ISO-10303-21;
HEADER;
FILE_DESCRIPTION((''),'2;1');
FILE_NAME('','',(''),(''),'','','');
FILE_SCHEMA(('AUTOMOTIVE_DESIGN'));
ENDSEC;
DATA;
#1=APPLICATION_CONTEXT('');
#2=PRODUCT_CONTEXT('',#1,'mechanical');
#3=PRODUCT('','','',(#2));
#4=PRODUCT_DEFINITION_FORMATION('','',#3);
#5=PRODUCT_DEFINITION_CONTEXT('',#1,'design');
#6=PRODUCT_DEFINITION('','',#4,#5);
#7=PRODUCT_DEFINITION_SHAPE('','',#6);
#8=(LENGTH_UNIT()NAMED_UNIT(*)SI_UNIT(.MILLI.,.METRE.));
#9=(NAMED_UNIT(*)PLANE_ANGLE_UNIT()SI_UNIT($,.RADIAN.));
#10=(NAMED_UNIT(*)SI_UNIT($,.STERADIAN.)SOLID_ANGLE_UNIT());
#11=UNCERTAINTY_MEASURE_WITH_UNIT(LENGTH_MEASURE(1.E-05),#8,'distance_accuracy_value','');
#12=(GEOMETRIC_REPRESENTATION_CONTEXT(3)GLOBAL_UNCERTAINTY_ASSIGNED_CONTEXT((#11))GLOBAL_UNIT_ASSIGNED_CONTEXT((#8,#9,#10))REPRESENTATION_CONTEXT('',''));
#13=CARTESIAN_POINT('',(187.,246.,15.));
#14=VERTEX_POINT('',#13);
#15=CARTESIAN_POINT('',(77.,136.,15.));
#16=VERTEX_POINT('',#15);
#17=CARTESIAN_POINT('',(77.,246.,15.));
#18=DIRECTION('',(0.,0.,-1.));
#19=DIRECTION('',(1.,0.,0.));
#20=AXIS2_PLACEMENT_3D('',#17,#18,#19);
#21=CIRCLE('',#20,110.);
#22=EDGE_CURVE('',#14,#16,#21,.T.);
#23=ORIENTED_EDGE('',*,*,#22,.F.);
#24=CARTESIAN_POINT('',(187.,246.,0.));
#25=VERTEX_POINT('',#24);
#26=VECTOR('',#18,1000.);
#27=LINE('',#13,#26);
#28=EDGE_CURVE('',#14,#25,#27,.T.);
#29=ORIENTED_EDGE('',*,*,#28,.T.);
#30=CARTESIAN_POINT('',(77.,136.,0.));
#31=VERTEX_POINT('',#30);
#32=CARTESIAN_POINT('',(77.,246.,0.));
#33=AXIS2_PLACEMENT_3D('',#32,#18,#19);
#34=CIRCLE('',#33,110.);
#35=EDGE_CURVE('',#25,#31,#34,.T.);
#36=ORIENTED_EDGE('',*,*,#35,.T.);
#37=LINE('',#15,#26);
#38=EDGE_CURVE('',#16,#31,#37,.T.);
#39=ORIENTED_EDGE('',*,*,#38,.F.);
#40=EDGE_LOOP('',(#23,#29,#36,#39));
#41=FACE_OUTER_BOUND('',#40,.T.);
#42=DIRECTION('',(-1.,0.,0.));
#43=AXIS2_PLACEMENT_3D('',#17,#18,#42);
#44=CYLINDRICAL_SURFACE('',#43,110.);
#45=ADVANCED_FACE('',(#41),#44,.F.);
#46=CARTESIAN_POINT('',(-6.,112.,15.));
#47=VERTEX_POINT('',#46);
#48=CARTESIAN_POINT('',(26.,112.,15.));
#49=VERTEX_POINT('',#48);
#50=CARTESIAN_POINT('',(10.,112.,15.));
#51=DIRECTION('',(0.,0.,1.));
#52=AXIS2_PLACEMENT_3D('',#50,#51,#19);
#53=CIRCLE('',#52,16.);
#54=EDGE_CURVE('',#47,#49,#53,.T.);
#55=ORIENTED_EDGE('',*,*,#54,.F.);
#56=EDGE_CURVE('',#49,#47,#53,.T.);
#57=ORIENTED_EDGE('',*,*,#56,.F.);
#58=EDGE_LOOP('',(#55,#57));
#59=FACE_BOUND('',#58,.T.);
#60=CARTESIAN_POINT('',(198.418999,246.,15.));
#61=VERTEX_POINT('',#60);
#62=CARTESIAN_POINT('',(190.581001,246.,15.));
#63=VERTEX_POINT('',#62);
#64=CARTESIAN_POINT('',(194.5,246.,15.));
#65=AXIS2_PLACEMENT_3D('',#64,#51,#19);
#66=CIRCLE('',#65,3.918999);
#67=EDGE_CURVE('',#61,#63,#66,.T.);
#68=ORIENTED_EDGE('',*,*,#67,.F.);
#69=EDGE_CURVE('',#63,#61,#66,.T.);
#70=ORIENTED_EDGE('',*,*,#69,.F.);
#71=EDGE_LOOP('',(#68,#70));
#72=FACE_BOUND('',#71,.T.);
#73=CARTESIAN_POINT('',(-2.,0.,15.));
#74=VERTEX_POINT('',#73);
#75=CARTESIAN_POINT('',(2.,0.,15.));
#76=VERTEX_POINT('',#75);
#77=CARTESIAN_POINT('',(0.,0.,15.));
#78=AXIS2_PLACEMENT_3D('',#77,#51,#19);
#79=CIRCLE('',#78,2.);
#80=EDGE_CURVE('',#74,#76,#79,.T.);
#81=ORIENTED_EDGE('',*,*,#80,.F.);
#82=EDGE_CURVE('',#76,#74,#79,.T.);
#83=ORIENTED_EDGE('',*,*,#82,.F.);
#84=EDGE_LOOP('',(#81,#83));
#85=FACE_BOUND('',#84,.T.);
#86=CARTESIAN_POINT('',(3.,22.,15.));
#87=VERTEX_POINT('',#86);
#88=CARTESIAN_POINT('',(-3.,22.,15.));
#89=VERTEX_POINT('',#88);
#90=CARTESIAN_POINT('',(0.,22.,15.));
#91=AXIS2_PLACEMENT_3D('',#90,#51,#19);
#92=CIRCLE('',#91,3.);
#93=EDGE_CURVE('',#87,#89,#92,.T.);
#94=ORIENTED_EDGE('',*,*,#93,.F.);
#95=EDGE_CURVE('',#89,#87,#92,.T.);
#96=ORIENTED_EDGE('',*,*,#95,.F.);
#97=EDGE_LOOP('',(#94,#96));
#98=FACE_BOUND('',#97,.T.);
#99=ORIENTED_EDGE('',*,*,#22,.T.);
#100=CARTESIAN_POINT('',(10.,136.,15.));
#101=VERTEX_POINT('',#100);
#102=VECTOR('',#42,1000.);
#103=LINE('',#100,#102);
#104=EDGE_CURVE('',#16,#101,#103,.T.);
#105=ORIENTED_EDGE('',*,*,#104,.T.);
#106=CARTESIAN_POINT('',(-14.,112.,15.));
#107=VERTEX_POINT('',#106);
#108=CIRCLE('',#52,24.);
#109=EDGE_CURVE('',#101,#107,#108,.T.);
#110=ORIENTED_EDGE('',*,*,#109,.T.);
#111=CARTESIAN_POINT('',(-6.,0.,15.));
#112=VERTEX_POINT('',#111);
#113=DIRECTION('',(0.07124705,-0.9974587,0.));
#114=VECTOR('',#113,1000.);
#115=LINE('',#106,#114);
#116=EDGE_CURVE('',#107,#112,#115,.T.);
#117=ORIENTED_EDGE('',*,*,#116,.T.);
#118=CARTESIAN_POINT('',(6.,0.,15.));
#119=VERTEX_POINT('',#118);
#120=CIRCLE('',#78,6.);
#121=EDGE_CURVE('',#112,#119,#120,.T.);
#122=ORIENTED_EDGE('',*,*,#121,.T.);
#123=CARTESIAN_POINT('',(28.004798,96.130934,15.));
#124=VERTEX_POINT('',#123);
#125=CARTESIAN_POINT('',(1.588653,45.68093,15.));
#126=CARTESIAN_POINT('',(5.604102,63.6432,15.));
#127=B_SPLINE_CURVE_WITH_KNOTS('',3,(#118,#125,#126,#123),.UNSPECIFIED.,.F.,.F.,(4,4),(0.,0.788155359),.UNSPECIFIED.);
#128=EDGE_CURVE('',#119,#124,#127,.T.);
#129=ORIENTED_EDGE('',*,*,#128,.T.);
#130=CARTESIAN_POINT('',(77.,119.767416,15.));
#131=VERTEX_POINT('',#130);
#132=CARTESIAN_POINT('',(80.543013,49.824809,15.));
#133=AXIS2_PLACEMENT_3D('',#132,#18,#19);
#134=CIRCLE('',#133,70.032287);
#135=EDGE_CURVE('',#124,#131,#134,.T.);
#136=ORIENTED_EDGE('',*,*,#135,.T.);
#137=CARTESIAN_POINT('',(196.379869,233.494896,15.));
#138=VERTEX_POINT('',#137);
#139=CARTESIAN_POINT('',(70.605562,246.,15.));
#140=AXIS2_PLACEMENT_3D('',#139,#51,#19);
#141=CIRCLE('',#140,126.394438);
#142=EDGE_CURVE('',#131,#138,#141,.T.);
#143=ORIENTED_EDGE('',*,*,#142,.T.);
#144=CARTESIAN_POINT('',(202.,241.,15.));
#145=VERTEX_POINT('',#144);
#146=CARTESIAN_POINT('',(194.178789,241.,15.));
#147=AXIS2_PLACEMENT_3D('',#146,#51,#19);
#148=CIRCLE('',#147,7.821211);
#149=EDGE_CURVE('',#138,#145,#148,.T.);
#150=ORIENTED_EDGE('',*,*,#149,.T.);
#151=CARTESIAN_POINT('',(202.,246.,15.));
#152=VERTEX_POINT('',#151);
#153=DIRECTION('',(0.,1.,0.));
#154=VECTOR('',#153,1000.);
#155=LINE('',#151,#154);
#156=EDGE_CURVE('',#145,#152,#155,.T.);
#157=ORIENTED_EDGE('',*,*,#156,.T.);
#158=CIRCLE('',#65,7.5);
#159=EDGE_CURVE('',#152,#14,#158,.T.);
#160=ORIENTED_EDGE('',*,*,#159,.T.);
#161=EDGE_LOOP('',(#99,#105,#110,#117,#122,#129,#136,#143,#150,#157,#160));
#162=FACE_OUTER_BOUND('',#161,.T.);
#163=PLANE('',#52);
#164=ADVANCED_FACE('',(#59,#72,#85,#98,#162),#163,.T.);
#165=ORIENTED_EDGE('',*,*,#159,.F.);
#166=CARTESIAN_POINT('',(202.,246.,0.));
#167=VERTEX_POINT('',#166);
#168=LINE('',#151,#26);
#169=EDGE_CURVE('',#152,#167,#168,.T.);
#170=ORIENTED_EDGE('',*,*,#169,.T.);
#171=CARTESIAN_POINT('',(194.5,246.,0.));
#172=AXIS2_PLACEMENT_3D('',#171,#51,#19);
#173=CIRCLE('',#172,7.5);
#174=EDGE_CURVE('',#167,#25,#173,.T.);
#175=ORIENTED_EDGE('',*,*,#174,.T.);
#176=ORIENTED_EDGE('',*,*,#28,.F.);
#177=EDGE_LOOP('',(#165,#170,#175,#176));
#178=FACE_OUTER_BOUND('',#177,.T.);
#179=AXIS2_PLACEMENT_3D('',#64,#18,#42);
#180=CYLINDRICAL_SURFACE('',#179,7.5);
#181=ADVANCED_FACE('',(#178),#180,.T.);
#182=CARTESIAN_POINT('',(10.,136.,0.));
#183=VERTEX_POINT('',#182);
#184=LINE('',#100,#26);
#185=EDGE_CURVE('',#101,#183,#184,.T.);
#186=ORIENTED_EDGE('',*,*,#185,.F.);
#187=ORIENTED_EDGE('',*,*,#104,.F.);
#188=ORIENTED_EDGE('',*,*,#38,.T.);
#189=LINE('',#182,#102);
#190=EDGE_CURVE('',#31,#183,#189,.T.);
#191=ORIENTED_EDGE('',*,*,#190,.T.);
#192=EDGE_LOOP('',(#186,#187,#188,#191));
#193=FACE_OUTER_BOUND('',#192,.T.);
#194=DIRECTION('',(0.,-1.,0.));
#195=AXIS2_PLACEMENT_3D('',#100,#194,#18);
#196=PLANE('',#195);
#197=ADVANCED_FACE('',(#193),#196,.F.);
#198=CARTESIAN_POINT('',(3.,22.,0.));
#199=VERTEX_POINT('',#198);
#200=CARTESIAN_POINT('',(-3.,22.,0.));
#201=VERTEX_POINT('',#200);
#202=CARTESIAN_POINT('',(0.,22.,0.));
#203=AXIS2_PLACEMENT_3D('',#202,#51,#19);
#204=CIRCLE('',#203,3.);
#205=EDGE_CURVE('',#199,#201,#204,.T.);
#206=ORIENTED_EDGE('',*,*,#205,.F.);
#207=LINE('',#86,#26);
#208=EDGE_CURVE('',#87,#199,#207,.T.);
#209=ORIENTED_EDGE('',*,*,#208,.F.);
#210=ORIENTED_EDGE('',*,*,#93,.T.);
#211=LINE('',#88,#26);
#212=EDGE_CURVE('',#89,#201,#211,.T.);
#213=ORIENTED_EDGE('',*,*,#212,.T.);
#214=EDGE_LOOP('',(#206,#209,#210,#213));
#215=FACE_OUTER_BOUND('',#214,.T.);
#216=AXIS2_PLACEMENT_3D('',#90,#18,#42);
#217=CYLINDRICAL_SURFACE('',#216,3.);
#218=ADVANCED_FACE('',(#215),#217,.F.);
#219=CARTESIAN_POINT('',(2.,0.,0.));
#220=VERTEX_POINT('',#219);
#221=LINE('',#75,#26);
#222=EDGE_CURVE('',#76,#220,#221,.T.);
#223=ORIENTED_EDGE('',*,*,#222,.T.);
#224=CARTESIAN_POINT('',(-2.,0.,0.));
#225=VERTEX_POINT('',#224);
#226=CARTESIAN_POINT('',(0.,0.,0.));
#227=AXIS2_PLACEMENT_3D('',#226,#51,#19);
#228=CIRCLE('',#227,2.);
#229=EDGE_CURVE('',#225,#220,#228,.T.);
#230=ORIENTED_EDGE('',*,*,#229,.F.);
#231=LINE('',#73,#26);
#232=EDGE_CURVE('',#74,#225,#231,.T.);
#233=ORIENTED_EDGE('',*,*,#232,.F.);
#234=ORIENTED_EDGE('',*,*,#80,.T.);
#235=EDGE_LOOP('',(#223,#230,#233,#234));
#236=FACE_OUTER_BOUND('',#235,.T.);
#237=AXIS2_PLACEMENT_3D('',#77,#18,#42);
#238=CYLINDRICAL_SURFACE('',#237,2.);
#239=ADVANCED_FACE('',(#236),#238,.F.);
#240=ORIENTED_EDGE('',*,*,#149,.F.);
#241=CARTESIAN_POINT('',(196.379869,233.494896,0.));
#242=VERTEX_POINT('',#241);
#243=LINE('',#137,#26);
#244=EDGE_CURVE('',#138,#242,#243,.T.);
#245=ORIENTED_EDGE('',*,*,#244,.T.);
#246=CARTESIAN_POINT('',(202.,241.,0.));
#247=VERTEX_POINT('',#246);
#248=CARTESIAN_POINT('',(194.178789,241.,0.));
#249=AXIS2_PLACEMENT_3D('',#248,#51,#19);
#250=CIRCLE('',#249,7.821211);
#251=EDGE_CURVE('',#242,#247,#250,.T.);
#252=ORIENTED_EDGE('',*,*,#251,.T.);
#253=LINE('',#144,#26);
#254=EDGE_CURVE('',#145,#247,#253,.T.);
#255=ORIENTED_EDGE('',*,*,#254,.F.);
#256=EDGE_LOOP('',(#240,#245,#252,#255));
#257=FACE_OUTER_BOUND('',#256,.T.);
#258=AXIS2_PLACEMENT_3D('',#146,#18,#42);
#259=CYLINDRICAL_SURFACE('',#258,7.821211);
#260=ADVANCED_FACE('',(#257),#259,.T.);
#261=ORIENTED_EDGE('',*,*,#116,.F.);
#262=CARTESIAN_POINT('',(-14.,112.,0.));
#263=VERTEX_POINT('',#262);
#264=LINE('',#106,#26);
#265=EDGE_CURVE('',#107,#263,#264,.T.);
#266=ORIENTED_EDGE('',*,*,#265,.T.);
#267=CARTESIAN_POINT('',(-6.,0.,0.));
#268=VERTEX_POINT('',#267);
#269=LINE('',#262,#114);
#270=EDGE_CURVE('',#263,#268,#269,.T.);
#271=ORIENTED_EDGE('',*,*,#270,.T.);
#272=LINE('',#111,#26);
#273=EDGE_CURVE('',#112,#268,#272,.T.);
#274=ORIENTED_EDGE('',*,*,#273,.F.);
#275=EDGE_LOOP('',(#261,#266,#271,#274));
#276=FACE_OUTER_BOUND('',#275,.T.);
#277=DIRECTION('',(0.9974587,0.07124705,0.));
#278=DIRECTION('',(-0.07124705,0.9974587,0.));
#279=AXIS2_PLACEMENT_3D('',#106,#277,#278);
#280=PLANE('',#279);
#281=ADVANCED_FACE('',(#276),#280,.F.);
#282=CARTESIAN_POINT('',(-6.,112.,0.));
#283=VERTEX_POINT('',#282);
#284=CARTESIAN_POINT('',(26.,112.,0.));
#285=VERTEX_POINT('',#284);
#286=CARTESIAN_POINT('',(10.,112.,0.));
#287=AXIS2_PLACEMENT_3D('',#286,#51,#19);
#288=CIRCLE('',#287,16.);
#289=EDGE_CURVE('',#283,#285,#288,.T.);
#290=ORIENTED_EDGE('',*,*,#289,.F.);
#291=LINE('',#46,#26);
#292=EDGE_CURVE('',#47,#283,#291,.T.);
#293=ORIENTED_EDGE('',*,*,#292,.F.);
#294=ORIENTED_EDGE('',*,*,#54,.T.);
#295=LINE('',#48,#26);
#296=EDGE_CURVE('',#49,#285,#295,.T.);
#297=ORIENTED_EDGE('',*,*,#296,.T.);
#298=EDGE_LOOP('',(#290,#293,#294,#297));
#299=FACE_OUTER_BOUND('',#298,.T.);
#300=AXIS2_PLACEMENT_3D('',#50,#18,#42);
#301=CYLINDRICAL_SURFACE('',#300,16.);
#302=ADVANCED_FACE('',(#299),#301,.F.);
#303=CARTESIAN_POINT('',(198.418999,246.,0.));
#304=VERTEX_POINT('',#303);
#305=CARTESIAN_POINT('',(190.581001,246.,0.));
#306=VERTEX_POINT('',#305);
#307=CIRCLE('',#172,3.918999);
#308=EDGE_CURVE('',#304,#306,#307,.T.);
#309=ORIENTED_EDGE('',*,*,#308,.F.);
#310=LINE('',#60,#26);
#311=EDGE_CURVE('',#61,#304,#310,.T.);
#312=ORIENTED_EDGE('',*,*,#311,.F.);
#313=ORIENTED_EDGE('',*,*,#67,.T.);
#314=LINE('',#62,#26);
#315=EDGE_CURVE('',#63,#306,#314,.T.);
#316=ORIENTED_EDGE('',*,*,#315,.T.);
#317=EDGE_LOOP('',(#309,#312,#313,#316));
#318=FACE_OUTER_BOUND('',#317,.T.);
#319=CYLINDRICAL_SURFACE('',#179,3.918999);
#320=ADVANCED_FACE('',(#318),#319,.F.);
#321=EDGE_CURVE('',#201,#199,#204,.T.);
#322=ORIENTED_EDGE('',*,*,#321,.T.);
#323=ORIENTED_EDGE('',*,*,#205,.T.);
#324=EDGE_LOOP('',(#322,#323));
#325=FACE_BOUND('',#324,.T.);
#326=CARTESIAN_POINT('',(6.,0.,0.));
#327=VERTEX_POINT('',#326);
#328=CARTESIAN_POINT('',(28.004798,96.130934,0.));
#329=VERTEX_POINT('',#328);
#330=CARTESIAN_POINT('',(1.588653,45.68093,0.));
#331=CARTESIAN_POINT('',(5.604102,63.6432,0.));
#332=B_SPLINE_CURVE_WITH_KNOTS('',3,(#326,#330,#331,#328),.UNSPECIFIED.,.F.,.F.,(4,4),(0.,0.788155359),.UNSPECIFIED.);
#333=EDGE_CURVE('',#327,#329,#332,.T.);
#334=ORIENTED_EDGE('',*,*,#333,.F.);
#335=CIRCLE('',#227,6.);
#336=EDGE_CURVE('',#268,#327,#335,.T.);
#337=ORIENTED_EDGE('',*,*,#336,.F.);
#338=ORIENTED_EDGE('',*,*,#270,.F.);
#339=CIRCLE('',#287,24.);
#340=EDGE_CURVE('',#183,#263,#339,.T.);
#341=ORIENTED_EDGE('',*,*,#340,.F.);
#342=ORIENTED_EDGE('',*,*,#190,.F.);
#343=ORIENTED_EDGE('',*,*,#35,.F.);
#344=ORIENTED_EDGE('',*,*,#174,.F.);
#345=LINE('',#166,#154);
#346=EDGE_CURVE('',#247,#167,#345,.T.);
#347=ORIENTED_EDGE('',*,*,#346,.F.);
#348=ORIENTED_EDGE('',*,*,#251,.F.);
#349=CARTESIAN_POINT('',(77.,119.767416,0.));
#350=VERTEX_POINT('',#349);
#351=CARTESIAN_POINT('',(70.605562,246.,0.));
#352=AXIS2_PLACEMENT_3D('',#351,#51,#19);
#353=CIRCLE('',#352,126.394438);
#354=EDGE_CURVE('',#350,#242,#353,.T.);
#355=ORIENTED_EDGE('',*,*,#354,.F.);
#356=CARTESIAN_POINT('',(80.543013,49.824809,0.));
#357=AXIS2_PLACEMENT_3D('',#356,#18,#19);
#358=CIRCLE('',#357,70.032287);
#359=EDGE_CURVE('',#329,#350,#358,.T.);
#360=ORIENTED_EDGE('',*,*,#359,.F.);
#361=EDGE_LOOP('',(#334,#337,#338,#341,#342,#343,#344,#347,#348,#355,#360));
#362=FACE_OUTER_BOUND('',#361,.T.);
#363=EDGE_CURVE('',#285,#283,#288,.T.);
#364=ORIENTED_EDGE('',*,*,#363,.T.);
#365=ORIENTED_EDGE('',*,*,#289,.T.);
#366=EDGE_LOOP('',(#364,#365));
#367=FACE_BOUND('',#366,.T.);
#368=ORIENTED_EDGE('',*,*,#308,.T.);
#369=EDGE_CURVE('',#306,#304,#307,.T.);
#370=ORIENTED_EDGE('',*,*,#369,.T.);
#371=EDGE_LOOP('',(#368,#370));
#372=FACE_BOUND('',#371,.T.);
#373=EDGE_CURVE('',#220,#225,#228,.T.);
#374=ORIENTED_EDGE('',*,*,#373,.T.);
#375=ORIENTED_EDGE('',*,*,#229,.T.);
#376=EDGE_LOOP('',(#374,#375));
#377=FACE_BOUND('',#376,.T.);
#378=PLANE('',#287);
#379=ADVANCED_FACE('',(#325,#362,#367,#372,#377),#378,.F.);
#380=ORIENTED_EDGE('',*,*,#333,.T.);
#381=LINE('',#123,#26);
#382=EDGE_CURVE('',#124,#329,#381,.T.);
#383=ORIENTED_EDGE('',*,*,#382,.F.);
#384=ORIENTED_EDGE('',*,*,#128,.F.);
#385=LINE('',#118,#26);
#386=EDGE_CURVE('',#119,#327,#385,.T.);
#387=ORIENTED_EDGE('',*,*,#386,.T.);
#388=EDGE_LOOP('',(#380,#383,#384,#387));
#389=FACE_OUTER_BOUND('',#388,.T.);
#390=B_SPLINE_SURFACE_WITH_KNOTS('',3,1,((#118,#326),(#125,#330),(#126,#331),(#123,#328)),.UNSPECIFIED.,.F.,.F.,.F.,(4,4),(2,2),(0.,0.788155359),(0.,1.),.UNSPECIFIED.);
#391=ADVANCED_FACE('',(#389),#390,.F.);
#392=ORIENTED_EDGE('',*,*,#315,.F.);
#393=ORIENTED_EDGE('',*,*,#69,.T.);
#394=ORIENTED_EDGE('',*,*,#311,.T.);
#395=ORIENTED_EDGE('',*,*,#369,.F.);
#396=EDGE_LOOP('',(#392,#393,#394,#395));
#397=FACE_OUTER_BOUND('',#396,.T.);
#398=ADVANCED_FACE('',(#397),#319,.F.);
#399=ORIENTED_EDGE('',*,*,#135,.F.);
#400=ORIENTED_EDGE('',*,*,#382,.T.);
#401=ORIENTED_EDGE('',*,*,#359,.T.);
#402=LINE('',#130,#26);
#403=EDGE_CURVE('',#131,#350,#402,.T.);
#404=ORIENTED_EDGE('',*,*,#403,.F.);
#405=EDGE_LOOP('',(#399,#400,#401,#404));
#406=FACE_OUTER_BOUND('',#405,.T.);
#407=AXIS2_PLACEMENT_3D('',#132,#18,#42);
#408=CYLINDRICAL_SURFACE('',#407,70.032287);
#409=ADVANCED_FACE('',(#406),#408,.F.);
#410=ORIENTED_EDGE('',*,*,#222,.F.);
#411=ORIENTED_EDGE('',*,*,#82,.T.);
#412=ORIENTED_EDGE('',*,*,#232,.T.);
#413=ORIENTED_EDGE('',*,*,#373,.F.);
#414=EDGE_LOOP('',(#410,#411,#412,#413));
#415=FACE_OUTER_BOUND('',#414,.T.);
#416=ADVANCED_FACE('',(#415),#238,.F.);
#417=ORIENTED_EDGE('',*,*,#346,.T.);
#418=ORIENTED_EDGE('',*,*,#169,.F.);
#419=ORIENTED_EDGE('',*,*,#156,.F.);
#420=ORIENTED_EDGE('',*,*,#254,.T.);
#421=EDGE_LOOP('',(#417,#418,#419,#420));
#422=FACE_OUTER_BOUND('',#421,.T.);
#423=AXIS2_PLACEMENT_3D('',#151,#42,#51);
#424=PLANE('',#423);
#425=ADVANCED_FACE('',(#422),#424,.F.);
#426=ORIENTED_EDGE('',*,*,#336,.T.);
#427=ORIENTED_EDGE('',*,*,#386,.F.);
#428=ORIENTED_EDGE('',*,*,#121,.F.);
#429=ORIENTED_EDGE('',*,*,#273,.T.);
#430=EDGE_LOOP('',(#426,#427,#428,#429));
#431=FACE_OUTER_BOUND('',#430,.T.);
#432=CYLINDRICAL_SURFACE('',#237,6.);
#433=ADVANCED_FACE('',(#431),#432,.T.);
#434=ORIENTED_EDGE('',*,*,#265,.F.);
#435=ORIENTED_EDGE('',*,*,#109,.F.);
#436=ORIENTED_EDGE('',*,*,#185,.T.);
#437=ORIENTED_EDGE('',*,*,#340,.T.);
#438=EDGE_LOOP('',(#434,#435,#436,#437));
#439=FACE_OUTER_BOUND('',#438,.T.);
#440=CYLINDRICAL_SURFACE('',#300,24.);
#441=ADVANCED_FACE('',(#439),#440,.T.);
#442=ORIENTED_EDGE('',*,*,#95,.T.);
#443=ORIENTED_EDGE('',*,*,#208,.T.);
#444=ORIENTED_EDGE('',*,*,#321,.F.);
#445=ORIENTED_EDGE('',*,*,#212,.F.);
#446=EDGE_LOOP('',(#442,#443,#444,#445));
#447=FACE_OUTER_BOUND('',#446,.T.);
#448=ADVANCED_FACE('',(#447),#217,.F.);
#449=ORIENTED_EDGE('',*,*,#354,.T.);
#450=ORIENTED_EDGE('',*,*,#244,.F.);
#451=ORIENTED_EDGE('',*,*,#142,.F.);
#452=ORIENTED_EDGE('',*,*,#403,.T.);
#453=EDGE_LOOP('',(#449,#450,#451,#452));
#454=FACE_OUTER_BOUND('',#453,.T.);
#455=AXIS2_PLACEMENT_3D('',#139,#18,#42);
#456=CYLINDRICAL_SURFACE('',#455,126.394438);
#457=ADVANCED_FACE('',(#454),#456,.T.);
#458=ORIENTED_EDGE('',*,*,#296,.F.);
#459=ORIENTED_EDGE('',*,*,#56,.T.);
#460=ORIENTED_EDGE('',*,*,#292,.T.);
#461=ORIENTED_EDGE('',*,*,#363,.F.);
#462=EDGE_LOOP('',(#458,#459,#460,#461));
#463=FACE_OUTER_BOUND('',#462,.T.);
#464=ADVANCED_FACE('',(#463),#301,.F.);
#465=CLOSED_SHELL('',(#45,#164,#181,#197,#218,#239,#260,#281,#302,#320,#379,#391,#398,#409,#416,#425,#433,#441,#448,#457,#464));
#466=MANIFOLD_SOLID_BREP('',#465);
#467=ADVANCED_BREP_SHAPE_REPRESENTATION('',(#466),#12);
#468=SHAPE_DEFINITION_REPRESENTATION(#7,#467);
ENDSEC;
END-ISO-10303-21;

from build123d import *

# Parameters (mm, degrees)
SKETCH_1_R      = 2
SKETCH_1_R_2    = 16
SKETCH_1_R_3    = 3.91899873
SKETCH_1_R_4    = 3
EXTRUDE_1_DEPTH = 15


with BuildPart() as part:
    # 草图1 → 凸台-拉伸1 (new body)
    with BuildSketch(Plane.XY):
        with BuildLine():
            Line((-14, 112), (-6, 0))
            ThreePointArc((-6, 0), (0, -6), (6, 0))
            add(Edge.make_bspline(
                [(6, 0), (1.588652615, 45.680929706), (5.604102499, 63.643200211), (28.004797731, 96.13093391)],
                knots=[0, 0, 0, 0, 0.788155359, 0.788155359, 0.788155359, 0.788155359], degree=3))
            ThreePointArc((28.004797731, 96.13093391), (50.113637924, 112.900750568), (77, 119.767416406))
            ThreePointArc((77, 119.767416406), (157.787149523, 154.485384951), (196.379869136, 233.494896157))
            ThreePointArc((196.379869136, 233.494896157), (200.439238403, 236.311917913), (202, 241))
            Line((202, 241), (202, 246))
            ThreePointArc((202, 246), (194.5, 253.5), (187, 246))
            ThreePointArc((187, 246), (154.781745931, 168.218254069), (77, 136))
            Line((77, 136), (10, 136))
            ThreePointArc((10, 136), (-6.970562748, 128.970562748), (-14, 112))
        make_face()
        Circle(SKETCH_1_R, mode=Mode.SUBTRACT)
        with Locations((10, 112)):
            Circle(SKETCH_1_R_2, mode=Mode.SUBTRACT)
        with Locations((194.5, 246)):
            Circle(SKETCH_1_R_3, mode=Mode.SUBTRACT)
        with Locations((0, 22)):
            Circle(SKETCH_1_R_4, mode=Mode.SUBTRACT)
    extrude(amount=EXTRUDE_1_DEPTH)


solid = part.part
